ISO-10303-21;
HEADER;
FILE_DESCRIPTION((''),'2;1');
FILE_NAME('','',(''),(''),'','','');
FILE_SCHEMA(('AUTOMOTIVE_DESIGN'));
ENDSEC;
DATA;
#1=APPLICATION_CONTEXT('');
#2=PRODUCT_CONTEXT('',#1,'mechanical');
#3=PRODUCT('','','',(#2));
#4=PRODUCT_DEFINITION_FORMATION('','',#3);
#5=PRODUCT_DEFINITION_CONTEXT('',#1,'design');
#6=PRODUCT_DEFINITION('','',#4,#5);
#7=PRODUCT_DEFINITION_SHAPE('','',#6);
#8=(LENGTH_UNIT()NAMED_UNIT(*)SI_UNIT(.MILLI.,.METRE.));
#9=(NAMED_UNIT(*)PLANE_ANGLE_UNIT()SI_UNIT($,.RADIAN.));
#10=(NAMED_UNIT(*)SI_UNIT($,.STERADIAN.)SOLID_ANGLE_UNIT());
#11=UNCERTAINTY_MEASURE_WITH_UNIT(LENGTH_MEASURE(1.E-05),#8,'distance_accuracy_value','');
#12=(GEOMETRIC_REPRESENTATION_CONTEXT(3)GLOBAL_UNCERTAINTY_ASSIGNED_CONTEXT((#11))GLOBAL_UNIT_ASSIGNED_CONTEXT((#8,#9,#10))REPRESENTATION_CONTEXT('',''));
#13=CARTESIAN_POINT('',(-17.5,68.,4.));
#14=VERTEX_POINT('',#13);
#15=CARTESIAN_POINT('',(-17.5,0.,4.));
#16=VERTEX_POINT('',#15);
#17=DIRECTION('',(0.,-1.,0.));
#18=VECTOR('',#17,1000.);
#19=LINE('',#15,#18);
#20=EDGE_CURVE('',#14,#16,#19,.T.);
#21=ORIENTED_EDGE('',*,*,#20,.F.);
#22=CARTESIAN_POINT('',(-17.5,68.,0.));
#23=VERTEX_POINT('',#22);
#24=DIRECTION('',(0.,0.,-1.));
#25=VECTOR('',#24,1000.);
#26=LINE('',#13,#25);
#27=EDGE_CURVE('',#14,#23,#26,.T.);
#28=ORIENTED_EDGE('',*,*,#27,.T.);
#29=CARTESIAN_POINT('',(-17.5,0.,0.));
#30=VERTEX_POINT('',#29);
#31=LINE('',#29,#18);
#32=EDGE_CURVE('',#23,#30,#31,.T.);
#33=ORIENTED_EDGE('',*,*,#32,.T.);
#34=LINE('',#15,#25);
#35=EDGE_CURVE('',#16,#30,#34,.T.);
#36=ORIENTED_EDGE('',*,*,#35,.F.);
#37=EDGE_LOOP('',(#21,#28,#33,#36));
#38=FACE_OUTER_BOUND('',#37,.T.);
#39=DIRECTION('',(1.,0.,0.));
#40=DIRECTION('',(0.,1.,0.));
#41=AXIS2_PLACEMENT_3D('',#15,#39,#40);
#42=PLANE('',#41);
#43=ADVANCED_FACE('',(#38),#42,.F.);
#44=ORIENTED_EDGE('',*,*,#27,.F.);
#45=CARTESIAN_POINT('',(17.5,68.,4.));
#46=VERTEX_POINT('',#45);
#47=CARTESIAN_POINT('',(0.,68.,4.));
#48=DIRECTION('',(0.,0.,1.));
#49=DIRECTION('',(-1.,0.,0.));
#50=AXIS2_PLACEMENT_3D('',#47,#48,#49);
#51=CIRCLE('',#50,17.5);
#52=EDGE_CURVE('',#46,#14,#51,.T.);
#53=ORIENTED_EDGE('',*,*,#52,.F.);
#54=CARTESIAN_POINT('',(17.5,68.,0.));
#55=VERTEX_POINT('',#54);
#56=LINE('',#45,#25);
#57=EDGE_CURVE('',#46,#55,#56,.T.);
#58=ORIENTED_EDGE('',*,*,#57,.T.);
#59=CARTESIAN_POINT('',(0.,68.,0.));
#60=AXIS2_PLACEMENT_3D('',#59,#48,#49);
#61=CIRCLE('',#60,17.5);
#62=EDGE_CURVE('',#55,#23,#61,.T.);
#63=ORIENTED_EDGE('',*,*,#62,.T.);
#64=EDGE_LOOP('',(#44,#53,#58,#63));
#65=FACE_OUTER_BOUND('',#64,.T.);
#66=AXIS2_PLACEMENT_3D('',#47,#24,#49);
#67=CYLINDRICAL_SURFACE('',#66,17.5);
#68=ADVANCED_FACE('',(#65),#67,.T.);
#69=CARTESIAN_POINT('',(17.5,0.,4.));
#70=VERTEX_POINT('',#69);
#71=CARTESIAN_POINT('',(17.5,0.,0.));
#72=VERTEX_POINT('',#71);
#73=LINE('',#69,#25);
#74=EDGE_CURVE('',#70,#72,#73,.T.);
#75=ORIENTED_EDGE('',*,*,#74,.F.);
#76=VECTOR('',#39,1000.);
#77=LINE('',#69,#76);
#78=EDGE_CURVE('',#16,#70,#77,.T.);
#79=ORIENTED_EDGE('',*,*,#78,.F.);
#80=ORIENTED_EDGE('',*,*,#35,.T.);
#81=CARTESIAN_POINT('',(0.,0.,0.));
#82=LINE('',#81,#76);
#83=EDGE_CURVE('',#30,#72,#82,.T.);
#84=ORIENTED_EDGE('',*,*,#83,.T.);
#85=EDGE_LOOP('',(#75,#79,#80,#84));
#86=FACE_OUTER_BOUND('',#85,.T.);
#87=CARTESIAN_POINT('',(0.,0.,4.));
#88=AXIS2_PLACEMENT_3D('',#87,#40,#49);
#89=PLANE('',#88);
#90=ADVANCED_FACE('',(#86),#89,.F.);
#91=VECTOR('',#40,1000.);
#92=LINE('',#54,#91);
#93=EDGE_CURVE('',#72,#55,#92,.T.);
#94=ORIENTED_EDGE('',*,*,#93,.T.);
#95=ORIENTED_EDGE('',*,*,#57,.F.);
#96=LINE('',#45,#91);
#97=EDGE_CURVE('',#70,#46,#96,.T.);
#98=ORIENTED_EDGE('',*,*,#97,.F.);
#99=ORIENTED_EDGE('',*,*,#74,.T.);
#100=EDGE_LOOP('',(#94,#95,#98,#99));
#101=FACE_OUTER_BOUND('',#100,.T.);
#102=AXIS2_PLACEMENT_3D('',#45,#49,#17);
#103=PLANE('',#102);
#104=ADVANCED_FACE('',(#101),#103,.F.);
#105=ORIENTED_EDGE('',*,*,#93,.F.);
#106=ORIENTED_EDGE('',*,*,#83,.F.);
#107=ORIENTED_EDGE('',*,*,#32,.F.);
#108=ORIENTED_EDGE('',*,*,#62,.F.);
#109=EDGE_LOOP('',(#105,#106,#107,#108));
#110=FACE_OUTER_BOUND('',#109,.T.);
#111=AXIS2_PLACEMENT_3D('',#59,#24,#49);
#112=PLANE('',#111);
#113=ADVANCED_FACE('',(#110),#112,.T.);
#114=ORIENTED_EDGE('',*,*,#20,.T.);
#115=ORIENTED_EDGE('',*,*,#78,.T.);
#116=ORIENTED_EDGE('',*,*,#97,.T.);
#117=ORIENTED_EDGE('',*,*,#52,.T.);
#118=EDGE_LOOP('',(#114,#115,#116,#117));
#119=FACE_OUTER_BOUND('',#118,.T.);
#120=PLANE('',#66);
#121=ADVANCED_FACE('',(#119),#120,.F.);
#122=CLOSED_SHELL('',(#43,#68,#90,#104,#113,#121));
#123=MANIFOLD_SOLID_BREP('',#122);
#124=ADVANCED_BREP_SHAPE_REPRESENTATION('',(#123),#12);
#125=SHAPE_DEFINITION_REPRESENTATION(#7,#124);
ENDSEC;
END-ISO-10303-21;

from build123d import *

# Parameters (mm, degrees)
EXTRUDE_1_DEPTH = 4


with BuildPart() as part:
    # 草图1 → 凸台-拉伸1 (new body)
    with BuildSketch(Plane.XY):
        with BuildLine():
            Line((0, 0), (-17.5, 0))
            Line((-17.5, 0), (-17.5, 68))
            ThreePointArc((-17.5, 68), (0, 85.5), (17.5, 68))
            Line((17.5, 68), (17.5, 0))
            Line((17.5, 0), (0, 0))
        make_face()
    extrude(amount=EXTRUDE_1_DEPTH)


solid = part.part
